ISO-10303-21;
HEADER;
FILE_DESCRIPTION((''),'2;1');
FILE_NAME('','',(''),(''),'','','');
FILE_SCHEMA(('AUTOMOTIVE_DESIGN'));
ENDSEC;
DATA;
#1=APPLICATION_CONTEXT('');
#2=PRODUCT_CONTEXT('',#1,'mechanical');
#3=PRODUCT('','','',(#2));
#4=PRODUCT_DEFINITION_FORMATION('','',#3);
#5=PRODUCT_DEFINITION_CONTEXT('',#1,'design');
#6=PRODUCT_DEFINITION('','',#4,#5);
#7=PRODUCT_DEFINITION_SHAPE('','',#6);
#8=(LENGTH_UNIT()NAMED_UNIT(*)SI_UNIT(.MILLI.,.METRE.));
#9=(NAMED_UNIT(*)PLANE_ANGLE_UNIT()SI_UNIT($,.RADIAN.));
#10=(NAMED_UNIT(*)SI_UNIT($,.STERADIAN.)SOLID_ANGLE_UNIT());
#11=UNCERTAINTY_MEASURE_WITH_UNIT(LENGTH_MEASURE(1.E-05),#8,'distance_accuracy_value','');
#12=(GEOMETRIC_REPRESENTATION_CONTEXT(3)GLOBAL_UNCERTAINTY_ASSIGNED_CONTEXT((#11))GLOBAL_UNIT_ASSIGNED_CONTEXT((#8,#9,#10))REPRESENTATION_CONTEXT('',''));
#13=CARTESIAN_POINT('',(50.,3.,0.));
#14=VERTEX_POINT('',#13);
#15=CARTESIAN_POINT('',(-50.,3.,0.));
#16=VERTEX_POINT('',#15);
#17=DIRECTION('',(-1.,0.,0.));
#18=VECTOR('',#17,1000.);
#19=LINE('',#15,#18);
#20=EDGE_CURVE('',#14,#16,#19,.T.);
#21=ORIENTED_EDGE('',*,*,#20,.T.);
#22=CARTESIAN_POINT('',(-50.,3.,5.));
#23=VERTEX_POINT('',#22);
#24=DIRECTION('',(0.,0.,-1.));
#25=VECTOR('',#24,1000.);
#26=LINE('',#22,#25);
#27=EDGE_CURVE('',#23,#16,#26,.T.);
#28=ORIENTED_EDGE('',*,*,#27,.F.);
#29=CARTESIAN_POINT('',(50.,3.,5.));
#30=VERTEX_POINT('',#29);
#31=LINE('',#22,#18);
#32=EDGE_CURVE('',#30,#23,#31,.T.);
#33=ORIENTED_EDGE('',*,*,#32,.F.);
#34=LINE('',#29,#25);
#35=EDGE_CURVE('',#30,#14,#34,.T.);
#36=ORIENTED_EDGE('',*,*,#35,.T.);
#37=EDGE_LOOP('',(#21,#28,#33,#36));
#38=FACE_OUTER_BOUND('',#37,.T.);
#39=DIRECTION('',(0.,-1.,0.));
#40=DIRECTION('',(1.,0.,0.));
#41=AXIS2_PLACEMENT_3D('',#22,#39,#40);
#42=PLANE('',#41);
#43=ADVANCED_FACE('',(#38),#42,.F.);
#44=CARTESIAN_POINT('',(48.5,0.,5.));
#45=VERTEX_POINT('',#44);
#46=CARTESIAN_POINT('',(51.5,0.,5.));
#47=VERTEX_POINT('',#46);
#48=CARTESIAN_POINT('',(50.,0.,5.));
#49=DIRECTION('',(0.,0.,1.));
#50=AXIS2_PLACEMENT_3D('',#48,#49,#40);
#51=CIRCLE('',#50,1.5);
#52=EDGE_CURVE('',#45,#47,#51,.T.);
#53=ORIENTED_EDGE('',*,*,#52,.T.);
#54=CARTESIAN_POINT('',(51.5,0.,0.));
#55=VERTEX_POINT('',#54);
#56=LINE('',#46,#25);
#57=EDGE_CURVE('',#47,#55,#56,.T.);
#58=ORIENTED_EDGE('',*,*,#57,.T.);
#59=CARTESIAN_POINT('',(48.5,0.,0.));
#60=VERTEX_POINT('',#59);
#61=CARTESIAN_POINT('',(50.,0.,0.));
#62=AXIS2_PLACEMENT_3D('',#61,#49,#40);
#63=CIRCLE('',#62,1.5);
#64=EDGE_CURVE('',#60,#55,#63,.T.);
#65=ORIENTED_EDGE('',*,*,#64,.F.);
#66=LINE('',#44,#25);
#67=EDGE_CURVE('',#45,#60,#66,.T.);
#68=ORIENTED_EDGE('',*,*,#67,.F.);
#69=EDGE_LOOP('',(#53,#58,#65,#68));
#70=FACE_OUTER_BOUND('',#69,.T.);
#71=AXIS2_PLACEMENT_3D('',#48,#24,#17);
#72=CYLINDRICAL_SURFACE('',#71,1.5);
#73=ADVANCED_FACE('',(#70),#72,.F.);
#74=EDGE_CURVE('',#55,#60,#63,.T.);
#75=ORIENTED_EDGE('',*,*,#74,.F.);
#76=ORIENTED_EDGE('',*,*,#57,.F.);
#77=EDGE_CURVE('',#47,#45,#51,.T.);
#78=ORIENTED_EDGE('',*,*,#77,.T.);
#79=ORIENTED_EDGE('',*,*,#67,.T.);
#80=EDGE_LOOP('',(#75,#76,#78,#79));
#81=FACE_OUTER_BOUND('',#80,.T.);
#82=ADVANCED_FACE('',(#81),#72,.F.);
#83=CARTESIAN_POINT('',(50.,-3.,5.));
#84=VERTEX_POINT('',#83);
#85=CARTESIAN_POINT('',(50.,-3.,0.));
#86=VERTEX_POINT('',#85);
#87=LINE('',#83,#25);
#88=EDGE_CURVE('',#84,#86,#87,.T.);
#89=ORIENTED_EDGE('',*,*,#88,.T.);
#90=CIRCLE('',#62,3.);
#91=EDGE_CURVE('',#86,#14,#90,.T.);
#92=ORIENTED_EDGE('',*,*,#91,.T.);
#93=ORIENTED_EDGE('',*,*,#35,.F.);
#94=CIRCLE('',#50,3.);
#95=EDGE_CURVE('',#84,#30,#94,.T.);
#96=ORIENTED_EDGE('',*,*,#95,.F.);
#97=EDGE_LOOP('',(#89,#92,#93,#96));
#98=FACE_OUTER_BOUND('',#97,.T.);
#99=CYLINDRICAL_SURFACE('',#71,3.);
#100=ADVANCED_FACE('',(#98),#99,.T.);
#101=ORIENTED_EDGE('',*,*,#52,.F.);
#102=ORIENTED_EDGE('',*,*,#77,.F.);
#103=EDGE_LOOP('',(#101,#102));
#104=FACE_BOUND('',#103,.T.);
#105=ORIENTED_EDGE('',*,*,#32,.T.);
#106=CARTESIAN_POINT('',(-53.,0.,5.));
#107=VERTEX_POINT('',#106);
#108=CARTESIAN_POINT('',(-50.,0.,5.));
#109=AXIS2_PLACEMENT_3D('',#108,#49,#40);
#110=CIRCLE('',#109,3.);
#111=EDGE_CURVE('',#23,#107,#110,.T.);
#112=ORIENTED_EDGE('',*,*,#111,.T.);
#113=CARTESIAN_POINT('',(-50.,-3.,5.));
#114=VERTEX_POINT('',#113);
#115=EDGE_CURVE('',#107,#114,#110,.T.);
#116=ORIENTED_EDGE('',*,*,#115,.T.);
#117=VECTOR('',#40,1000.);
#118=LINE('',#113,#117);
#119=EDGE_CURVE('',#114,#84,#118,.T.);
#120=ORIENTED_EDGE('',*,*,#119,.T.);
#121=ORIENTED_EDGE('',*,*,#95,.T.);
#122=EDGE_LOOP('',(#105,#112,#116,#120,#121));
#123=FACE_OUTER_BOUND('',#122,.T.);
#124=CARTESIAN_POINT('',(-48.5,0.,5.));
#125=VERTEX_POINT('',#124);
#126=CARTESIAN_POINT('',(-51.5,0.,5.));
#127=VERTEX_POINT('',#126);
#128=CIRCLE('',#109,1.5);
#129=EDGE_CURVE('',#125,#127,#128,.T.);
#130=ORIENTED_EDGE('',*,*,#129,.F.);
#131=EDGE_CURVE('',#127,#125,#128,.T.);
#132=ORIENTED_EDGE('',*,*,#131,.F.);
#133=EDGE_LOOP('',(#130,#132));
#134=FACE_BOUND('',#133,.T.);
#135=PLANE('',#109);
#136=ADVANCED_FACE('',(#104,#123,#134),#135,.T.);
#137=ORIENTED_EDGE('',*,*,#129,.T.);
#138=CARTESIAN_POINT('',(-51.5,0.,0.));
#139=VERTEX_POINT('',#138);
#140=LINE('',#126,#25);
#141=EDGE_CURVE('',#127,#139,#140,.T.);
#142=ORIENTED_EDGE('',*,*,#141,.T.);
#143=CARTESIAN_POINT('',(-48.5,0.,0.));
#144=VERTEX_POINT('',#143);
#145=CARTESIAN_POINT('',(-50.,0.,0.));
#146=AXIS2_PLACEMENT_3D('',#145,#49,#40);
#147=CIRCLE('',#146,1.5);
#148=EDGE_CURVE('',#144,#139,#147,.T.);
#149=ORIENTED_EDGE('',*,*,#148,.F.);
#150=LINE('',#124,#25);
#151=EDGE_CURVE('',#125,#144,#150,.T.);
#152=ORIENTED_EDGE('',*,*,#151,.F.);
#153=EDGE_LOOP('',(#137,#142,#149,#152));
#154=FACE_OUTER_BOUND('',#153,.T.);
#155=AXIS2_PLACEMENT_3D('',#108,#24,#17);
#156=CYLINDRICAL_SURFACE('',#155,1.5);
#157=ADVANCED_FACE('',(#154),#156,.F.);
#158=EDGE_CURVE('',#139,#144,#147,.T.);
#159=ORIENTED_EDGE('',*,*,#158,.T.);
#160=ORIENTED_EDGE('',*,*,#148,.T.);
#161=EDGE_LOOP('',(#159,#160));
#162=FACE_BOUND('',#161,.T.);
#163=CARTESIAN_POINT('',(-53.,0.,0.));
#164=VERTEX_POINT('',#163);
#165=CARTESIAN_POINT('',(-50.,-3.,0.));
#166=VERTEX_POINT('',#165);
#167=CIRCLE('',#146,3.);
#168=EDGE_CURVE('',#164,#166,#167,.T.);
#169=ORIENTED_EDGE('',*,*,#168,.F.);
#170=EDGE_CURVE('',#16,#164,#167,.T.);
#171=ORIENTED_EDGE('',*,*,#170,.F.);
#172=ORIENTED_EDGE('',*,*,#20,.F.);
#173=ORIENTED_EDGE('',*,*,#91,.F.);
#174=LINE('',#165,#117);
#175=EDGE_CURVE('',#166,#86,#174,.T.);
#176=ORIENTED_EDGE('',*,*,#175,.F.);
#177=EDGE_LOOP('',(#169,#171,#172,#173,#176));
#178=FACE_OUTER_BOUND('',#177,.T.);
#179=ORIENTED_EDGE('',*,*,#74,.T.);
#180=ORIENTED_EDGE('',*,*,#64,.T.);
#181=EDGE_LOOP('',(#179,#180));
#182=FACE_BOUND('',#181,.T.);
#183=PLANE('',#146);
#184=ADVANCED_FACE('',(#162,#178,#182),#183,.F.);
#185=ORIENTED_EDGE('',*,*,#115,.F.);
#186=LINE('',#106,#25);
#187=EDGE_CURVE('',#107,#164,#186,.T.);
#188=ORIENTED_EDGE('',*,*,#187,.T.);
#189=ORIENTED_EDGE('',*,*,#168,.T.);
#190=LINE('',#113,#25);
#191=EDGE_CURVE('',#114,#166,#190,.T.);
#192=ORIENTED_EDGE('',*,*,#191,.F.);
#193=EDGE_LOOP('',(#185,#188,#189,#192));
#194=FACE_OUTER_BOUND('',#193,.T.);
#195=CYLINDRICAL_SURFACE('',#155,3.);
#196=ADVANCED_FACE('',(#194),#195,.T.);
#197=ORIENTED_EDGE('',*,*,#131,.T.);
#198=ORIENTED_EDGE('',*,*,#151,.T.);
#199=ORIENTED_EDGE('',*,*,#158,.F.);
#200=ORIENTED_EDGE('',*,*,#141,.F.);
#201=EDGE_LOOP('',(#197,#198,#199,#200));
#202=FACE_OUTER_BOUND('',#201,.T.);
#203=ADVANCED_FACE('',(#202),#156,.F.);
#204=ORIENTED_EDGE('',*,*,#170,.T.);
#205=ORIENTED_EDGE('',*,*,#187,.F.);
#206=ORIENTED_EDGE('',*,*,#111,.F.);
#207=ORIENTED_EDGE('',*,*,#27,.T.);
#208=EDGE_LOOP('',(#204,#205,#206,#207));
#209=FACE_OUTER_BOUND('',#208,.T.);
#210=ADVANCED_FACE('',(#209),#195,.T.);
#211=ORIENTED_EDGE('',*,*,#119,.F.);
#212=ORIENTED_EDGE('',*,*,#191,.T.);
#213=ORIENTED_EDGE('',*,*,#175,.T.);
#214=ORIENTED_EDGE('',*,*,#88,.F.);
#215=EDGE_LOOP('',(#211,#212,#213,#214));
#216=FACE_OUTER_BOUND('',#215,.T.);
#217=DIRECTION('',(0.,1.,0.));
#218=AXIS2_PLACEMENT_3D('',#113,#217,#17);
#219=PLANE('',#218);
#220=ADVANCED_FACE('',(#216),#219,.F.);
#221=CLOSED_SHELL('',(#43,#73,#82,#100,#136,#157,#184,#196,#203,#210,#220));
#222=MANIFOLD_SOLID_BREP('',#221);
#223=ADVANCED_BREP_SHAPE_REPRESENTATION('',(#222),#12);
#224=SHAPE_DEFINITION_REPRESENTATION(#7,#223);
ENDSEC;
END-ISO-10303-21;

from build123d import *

# Parameters (mm, degrees)
LINK_PROFILE_SKETCH_R        = 1.5
LINK_BAR_100_CTRS_2X_3_DEPTH = 5


with BuildPart() as part:
    # Link Profile Sketch → Link Bar 100 Ctrs 2xØ3 (new body)
    with BuildSketch(Plane.XY):
        with BuildLine():
            Line((-50, 3), (50, 3))
            ThreePointArc((50, 3), (53, 0), (50, -3))
            Line((50, -3), (-50, -3))
            ThreePointArc((-50, -3), (-53, 0), (-50, 3))
        make_face()
        with Locations((-50, 0)):
            Circle(LINK_PROFILE_SKETCH_R, mode=Mode.SUBTRACT)
        with Locations((50, 0)):
            Circle(LINK_PROFILE_SKETCH_R, mode=Mode.SUBTRACT)
    extrude(amount=LINK_BAR_100_CTRS_2X_3_DEPTH)


solid = part.part
